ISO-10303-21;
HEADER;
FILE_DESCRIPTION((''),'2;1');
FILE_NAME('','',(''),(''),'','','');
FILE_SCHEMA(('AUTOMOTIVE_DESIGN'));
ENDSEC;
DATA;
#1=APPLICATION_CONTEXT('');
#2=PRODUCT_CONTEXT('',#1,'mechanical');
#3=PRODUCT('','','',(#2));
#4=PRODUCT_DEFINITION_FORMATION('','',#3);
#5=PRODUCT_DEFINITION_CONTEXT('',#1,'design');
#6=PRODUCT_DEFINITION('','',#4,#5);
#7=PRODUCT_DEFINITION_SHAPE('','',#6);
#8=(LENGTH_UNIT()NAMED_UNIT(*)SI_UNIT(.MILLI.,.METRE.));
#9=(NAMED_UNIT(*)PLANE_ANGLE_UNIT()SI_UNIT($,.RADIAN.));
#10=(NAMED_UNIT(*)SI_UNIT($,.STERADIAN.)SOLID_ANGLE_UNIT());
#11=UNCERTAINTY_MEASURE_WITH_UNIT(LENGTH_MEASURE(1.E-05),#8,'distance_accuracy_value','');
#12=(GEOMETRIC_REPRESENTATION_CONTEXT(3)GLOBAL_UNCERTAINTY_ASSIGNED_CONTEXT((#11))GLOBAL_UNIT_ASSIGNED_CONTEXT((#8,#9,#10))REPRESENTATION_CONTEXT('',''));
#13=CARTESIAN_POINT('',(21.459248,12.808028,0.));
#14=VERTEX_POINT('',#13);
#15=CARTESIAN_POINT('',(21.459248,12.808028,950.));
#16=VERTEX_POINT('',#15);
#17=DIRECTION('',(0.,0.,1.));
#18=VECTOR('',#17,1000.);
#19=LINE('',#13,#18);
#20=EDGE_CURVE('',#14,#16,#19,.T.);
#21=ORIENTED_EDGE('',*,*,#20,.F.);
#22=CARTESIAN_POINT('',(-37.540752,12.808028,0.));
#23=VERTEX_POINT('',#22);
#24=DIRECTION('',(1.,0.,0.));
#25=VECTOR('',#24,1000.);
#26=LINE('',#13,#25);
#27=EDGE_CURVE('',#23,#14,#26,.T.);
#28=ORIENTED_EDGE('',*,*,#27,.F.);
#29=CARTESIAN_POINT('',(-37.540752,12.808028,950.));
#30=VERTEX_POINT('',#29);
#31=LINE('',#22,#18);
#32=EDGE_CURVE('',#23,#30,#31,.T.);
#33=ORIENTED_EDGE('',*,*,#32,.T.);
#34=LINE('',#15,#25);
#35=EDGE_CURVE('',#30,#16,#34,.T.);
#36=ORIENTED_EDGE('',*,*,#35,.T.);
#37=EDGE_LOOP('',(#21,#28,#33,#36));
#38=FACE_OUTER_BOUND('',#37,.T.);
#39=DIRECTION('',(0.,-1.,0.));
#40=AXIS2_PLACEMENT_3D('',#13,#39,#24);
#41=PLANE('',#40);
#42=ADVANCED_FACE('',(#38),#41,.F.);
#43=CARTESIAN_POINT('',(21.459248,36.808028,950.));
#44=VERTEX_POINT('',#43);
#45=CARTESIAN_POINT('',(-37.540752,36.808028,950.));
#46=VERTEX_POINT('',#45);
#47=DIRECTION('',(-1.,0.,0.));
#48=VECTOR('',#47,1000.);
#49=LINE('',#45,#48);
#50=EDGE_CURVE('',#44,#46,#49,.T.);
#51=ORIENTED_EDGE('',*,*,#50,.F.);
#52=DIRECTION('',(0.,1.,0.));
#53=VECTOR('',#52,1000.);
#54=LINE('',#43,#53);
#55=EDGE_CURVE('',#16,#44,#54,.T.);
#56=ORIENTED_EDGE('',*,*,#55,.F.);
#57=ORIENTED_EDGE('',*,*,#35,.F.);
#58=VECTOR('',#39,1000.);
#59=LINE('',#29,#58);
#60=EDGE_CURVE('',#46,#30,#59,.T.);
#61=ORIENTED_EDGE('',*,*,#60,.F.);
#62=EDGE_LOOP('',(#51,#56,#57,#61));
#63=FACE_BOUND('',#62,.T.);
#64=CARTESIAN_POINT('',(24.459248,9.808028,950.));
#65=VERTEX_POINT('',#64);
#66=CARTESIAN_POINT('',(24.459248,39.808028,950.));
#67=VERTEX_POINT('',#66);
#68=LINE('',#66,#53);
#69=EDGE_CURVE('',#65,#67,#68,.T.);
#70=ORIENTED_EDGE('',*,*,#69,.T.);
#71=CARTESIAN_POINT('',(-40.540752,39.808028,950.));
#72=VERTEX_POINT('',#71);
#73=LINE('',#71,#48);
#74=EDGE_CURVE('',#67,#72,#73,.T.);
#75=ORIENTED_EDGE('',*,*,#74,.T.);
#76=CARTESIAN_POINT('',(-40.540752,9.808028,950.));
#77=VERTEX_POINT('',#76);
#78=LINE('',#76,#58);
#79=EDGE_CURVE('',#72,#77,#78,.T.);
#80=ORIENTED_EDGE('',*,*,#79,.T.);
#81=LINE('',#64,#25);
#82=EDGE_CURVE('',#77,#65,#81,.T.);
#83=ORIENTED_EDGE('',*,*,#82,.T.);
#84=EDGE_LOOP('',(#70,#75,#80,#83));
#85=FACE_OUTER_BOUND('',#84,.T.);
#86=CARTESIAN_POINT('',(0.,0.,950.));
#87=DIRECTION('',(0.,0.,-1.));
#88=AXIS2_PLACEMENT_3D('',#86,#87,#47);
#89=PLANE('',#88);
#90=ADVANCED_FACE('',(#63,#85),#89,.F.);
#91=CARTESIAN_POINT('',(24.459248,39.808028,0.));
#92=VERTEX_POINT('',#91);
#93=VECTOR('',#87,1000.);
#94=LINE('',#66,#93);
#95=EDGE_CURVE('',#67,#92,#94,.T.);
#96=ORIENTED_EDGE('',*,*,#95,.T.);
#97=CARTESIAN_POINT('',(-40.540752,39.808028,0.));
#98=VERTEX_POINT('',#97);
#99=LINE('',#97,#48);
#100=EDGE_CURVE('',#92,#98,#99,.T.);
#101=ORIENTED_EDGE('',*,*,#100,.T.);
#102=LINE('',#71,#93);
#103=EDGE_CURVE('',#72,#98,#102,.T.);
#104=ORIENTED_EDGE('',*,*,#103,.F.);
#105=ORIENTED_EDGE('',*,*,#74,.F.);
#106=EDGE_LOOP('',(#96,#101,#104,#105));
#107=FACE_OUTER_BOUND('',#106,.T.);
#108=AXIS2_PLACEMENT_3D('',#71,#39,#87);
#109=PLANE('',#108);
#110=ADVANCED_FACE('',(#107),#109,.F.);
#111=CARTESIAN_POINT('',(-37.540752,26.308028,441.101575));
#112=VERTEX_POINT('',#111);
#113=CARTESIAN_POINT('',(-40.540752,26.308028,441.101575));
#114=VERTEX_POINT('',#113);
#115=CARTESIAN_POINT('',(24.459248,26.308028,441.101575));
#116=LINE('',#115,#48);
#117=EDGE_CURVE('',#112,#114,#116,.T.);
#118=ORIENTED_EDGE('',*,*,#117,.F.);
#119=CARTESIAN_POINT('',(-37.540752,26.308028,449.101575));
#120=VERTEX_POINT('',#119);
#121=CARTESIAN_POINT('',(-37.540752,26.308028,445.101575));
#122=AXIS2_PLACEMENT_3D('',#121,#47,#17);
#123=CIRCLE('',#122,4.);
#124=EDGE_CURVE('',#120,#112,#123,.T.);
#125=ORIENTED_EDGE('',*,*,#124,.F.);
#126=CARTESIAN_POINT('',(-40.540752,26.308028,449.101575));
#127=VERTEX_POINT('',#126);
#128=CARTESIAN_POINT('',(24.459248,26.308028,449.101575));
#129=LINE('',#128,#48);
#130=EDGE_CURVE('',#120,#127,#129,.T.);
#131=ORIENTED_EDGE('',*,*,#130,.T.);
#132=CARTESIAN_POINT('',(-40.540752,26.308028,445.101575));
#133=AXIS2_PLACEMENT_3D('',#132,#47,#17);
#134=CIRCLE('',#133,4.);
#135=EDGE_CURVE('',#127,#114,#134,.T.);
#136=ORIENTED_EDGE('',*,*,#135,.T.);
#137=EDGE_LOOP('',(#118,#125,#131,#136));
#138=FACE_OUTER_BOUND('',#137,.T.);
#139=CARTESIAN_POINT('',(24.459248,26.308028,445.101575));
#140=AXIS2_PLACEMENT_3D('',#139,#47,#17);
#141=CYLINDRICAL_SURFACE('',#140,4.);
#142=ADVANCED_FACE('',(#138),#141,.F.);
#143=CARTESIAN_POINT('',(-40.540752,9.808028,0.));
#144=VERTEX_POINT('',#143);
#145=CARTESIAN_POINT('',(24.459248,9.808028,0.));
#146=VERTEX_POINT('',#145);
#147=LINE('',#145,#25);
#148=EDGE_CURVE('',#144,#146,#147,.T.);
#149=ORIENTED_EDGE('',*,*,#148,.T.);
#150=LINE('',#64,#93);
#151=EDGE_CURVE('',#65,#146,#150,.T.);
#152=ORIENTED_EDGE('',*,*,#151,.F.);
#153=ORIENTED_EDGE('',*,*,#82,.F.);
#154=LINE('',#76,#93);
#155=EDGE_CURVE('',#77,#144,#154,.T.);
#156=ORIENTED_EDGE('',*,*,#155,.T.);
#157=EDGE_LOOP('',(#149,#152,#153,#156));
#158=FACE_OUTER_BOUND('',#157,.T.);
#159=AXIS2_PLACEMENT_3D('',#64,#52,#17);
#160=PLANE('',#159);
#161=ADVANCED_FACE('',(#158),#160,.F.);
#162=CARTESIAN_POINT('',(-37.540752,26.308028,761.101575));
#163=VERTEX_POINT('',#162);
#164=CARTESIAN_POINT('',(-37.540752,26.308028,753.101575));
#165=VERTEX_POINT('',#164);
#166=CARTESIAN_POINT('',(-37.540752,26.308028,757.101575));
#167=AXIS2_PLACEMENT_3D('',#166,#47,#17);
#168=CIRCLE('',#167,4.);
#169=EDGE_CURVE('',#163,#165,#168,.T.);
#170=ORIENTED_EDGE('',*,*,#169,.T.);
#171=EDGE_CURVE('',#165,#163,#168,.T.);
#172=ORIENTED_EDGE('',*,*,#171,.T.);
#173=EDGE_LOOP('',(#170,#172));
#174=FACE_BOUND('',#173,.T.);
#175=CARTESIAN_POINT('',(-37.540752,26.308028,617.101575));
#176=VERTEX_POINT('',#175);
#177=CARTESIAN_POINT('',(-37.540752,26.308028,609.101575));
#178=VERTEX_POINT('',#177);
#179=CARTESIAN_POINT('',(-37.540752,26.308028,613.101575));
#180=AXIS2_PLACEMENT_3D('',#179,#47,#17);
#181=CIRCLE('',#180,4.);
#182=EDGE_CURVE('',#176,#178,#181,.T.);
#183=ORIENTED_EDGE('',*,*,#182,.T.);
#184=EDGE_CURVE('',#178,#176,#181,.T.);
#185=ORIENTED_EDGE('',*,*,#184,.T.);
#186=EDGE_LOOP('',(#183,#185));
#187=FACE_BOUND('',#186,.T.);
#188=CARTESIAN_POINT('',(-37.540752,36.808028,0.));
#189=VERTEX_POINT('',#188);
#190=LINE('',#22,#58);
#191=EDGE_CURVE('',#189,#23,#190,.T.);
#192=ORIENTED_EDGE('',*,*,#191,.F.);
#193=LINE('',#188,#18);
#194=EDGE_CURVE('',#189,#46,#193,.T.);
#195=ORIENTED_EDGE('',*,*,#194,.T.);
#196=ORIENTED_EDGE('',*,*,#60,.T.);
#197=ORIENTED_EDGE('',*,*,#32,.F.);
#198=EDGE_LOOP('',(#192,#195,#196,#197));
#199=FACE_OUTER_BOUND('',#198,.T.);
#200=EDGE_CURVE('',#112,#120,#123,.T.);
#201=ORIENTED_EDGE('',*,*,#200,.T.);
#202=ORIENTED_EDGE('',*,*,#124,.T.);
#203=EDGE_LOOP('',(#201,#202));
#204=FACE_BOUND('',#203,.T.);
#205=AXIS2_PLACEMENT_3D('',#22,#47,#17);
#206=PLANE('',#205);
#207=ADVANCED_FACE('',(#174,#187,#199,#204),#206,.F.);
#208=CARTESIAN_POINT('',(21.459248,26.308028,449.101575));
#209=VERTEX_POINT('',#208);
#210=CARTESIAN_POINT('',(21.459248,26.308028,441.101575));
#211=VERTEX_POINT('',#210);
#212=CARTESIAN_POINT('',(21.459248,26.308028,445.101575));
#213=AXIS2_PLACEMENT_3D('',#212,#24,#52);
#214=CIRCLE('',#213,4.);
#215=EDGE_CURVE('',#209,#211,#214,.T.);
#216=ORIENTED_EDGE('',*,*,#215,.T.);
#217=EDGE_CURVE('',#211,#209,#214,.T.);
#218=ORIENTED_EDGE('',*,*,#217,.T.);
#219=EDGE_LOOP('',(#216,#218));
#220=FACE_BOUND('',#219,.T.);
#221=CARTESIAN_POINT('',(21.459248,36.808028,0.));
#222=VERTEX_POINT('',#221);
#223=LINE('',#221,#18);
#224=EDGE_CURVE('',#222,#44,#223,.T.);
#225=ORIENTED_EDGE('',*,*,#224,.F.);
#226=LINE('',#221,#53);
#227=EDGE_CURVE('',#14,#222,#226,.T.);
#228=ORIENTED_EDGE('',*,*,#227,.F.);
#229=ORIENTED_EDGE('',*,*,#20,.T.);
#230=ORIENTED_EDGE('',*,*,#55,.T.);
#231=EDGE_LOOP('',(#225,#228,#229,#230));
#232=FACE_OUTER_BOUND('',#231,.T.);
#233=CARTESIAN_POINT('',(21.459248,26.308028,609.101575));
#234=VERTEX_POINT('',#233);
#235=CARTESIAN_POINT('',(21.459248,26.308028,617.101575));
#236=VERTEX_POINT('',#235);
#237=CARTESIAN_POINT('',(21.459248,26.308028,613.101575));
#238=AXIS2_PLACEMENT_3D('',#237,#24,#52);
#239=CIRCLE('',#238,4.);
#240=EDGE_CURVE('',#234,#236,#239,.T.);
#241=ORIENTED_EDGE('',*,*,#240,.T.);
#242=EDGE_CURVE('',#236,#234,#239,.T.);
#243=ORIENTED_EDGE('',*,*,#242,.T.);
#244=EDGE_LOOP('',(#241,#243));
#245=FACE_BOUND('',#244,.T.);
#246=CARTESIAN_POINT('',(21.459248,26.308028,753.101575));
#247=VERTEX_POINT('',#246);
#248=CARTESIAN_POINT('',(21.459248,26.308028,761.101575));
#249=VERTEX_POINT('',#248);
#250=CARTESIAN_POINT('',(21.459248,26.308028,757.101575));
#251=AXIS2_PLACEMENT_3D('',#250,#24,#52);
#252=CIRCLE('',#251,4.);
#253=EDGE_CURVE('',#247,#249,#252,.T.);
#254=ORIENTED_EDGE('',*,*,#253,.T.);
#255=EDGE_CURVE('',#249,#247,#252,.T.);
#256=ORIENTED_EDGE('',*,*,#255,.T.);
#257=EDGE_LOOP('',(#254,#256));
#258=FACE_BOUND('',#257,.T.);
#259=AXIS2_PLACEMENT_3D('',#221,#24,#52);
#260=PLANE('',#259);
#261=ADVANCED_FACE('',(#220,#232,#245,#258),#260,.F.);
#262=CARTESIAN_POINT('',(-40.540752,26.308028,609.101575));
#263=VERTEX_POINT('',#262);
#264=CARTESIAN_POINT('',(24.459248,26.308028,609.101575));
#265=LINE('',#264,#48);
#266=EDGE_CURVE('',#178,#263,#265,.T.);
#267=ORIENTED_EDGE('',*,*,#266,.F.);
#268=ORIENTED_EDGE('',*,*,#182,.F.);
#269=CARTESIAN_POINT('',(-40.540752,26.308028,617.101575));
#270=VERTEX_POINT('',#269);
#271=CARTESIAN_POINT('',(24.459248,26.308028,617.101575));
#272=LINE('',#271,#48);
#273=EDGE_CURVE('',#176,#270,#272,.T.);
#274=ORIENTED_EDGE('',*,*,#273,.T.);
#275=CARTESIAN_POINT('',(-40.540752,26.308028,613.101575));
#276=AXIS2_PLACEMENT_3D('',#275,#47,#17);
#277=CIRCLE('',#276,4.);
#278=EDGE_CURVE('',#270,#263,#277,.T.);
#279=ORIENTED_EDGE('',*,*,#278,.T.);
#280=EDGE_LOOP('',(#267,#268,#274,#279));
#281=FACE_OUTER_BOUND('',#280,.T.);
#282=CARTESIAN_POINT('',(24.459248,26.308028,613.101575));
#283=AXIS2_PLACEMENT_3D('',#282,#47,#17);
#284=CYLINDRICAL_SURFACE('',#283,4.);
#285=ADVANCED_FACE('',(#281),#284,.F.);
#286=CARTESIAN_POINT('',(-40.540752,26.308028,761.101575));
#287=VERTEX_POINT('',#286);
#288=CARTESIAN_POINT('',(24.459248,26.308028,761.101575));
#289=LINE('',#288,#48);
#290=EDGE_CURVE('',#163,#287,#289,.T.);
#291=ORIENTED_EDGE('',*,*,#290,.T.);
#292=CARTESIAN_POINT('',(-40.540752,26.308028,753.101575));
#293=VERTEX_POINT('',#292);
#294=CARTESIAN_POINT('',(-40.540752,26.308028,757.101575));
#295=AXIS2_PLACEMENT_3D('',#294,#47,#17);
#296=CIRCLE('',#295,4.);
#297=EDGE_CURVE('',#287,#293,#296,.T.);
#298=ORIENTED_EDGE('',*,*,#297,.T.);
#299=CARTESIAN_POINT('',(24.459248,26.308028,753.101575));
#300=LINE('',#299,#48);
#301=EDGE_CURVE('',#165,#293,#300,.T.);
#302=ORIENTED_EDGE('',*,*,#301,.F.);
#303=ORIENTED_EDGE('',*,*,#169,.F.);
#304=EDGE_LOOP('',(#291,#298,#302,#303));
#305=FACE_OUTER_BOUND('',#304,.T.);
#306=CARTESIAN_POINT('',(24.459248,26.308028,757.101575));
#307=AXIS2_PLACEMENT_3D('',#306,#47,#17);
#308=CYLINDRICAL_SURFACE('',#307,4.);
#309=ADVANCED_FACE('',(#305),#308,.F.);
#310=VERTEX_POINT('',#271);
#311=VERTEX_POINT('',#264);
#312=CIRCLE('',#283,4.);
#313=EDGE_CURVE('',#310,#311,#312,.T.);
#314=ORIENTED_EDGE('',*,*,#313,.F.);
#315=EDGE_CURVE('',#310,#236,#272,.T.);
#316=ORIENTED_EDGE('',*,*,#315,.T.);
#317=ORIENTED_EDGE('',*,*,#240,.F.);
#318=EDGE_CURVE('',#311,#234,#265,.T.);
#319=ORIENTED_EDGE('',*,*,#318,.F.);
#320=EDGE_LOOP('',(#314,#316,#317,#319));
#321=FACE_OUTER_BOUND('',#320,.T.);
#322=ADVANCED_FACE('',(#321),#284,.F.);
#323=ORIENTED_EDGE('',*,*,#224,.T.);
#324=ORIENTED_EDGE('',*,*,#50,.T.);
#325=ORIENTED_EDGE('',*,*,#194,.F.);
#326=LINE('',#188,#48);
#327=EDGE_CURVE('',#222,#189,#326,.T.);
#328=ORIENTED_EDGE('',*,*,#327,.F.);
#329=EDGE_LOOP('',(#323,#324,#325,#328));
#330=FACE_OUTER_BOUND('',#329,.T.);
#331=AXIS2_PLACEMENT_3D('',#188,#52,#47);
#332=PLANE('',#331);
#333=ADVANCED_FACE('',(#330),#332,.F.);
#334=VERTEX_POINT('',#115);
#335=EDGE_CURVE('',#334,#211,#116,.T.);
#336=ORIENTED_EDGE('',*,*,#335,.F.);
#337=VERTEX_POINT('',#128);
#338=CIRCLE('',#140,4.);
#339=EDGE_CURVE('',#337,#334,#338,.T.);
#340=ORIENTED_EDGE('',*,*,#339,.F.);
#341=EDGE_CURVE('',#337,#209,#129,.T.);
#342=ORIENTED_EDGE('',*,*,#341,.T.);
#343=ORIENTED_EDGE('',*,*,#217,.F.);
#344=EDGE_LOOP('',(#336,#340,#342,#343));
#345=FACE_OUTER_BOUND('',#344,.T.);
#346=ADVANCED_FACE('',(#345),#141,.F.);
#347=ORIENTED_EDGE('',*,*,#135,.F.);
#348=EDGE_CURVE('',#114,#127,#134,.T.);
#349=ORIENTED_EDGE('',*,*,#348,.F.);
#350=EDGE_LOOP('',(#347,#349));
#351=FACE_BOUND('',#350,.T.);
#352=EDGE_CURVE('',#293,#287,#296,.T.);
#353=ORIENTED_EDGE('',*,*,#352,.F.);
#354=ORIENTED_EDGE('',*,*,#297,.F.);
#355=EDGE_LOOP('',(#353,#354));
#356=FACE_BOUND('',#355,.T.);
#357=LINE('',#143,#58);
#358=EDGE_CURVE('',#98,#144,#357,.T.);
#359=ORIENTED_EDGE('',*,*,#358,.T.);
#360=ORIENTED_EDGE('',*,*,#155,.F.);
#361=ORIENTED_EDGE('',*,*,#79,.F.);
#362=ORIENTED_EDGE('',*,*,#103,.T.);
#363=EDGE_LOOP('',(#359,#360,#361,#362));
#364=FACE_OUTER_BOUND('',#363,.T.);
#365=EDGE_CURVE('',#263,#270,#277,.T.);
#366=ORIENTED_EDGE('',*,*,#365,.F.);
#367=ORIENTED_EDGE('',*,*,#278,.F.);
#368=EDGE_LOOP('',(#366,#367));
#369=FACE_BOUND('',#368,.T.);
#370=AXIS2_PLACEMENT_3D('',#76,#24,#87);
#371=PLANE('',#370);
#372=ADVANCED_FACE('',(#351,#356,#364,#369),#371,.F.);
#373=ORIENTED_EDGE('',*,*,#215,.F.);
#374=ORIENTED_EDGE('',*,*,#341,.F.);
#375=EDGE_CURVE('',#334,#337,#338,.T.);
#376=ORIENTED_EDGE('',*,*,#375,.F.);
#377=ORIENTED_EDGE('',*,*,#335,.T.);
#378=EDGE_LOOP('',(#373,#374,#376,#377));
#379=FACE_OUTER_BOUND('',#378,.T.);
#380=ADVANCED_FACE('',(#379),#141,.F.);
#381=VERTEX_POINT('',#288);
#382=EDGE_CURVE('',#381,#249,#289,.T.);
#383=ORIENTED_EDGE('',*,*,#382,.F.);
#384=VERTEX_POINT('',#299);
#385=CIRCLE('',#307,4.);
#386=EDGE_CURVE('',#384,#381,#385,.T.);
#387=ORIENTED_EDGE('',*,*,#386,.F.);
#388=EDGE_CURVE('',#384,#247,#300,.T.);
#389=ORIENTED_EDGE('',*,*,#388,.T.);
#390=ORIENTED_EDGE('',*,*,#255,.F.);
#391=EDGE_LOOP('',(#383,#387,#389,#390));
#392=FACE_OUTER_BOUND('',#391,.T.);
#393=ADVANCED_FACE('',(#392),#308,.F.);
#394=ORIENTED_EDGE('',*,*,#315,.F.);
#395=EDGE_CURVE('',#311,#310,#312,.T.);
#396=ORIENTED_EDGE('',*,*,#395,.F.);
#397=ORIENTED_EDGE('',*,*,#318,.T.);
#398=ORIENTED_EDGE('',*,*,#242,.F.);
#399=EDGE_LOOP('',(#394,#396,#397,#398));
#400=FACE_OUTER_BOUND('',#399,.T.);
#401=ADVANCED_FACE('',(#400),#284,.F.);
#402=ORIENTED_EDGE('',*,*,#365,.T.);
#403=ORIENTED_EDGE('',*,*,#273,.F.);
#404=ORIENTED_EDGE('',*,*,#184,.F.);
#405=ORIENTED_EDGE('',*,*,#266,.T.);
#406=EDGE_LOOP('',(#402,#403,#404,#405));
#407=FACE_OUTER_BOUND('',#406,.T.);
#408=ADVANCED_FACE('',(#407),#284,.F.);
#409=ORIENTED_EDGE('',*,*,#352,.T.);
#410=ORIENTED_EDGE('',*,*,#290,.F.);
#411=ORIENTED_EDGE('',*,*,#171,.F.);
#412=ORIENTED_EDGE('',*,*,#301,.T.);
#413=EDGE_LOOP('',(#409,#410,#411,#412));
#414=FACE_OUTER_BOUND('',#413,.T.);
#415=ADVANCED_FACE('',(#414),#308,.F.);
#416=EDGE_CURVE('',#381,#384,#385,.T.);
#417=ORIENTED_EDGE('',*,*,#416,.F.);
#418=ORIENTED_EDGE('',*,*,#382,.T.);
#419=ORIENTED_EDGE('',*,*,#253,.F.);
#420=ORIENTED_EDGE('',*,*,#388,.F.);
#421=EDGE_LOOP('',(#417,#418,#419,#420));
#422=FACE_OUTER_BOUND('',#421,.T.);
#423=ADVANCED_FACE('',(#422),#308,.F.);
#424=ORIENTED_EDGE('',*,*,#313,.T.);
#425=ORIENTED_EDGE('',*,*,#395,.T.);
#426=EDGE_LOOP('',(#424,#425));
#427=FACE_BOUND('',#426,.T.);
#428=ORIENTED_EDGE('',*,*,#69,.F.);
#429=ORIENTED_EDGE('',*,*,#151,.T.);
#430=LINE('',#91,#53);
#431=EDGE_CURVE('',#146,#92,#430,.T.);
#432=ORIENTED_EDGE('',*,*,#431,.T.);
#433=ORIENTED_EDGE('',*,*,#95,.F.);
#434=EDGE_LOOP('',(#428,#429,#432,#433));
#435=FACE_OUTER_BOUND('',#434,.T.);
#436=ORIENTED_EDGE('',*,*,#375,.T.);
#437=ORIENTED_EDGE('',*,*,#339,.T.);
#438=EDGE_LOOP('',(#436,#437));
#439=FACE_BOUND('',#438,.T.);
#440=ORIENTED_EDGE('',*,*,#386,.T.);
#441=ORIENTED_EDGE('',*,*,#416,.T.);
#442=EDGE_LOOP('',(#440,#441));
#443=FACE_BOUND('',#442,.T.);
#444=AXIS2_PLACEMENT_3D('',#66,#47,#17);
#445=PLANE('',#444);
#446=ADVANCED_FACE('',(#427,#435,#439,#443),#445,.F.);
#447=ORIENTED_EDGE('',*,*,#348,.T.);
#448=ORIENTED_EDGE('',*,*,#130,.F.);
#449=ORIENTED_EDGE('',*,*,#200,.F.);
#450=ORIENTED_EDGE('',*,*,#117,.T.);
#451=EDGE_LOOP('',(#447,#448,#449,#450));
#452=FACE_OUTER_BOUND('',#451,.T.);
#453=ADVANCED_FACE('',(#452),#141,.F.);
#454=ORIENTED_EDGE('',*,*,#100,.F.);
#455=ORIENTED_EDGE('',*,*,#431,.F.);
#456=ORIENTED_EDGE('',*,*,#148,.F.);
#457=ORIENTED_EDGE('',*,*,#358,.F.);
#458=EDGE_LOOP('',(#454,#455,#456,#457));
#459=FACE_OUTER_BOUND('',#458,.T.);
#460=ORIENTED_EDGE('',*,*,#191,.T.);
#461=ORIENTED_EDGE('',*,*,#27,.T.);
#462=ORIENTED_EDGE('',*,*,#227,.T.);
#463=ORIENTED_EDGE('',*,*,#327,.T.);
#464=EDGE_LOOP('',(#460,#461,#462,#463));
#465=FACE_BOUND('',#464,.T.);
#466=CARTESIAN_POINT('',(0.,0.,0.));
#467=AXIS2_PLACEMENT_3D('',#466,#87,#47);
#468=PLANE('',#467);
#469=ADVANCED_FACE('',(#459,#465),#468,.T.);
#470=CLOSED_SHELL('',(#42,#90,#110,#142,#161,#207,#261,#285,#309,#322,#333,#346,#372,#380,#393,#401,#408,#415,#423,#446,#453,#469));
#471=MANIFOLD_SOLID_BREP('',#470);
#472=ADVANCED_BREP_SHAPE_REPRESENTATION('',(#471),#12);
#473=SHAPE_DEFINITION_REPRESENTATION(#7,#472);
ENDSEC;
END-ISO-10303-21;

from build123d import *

# Parameters (mm, degrees)
SKETCH1_W           = 65
SKETCH1_H           = 30
BOSS_EXTRUDE1_DEPTH = 950
SKETCH2_W           = 59
SKETCH2_H           = 24
CUT_EXTRUDE1_DEPTH  = 950
SKETCH5_R           = 4
CUT_EXTRUDE2_DEPTH  = 954.05282071


with BuildPart() as part:
    # Sketch1 → Boss-Extrude1 (new body)
    with BuildSketch(Plane.XY):
        with Locations((-8.040751589, 24.808027615)):
            Rectangle(SKETCH1_W, SKETCH1_H)
    extrude(amount=BOSS_EXTRUDE1_DEPTH)

    # Sketch2 → Cut-Extrude1 (cut)
    with BuildSketch(Plane.XY.offset(950)):
        with Locations((-8.040751589, 24.808027615)):
            Rectangle(SKETCH2_W, SKETCH2_H)
    extrude(amount=-CUT_EXTRUDE1_DEPTH, mode=Mode.SUBTRACT)

    # Sketch5 → Cut-Extrude2 (cut, through all)
    with BuildSketch(Plane.ZY.offset(40.540751589)):
        with Locations((445.101574912, 26.308027615)):
            Circle(SKETCH5_R)
        with Locations((613.101574912, 26.308027615)):
            Circle(SKETCH5_R)
        with Locations((757.101574912, 26.308027615)):
            Circle(SKETCH5_R)
    extrude(amount=-CUT_EXTRUDE2_DEPTH, mode=Mode.SUBTRACT)


solid = part.part
